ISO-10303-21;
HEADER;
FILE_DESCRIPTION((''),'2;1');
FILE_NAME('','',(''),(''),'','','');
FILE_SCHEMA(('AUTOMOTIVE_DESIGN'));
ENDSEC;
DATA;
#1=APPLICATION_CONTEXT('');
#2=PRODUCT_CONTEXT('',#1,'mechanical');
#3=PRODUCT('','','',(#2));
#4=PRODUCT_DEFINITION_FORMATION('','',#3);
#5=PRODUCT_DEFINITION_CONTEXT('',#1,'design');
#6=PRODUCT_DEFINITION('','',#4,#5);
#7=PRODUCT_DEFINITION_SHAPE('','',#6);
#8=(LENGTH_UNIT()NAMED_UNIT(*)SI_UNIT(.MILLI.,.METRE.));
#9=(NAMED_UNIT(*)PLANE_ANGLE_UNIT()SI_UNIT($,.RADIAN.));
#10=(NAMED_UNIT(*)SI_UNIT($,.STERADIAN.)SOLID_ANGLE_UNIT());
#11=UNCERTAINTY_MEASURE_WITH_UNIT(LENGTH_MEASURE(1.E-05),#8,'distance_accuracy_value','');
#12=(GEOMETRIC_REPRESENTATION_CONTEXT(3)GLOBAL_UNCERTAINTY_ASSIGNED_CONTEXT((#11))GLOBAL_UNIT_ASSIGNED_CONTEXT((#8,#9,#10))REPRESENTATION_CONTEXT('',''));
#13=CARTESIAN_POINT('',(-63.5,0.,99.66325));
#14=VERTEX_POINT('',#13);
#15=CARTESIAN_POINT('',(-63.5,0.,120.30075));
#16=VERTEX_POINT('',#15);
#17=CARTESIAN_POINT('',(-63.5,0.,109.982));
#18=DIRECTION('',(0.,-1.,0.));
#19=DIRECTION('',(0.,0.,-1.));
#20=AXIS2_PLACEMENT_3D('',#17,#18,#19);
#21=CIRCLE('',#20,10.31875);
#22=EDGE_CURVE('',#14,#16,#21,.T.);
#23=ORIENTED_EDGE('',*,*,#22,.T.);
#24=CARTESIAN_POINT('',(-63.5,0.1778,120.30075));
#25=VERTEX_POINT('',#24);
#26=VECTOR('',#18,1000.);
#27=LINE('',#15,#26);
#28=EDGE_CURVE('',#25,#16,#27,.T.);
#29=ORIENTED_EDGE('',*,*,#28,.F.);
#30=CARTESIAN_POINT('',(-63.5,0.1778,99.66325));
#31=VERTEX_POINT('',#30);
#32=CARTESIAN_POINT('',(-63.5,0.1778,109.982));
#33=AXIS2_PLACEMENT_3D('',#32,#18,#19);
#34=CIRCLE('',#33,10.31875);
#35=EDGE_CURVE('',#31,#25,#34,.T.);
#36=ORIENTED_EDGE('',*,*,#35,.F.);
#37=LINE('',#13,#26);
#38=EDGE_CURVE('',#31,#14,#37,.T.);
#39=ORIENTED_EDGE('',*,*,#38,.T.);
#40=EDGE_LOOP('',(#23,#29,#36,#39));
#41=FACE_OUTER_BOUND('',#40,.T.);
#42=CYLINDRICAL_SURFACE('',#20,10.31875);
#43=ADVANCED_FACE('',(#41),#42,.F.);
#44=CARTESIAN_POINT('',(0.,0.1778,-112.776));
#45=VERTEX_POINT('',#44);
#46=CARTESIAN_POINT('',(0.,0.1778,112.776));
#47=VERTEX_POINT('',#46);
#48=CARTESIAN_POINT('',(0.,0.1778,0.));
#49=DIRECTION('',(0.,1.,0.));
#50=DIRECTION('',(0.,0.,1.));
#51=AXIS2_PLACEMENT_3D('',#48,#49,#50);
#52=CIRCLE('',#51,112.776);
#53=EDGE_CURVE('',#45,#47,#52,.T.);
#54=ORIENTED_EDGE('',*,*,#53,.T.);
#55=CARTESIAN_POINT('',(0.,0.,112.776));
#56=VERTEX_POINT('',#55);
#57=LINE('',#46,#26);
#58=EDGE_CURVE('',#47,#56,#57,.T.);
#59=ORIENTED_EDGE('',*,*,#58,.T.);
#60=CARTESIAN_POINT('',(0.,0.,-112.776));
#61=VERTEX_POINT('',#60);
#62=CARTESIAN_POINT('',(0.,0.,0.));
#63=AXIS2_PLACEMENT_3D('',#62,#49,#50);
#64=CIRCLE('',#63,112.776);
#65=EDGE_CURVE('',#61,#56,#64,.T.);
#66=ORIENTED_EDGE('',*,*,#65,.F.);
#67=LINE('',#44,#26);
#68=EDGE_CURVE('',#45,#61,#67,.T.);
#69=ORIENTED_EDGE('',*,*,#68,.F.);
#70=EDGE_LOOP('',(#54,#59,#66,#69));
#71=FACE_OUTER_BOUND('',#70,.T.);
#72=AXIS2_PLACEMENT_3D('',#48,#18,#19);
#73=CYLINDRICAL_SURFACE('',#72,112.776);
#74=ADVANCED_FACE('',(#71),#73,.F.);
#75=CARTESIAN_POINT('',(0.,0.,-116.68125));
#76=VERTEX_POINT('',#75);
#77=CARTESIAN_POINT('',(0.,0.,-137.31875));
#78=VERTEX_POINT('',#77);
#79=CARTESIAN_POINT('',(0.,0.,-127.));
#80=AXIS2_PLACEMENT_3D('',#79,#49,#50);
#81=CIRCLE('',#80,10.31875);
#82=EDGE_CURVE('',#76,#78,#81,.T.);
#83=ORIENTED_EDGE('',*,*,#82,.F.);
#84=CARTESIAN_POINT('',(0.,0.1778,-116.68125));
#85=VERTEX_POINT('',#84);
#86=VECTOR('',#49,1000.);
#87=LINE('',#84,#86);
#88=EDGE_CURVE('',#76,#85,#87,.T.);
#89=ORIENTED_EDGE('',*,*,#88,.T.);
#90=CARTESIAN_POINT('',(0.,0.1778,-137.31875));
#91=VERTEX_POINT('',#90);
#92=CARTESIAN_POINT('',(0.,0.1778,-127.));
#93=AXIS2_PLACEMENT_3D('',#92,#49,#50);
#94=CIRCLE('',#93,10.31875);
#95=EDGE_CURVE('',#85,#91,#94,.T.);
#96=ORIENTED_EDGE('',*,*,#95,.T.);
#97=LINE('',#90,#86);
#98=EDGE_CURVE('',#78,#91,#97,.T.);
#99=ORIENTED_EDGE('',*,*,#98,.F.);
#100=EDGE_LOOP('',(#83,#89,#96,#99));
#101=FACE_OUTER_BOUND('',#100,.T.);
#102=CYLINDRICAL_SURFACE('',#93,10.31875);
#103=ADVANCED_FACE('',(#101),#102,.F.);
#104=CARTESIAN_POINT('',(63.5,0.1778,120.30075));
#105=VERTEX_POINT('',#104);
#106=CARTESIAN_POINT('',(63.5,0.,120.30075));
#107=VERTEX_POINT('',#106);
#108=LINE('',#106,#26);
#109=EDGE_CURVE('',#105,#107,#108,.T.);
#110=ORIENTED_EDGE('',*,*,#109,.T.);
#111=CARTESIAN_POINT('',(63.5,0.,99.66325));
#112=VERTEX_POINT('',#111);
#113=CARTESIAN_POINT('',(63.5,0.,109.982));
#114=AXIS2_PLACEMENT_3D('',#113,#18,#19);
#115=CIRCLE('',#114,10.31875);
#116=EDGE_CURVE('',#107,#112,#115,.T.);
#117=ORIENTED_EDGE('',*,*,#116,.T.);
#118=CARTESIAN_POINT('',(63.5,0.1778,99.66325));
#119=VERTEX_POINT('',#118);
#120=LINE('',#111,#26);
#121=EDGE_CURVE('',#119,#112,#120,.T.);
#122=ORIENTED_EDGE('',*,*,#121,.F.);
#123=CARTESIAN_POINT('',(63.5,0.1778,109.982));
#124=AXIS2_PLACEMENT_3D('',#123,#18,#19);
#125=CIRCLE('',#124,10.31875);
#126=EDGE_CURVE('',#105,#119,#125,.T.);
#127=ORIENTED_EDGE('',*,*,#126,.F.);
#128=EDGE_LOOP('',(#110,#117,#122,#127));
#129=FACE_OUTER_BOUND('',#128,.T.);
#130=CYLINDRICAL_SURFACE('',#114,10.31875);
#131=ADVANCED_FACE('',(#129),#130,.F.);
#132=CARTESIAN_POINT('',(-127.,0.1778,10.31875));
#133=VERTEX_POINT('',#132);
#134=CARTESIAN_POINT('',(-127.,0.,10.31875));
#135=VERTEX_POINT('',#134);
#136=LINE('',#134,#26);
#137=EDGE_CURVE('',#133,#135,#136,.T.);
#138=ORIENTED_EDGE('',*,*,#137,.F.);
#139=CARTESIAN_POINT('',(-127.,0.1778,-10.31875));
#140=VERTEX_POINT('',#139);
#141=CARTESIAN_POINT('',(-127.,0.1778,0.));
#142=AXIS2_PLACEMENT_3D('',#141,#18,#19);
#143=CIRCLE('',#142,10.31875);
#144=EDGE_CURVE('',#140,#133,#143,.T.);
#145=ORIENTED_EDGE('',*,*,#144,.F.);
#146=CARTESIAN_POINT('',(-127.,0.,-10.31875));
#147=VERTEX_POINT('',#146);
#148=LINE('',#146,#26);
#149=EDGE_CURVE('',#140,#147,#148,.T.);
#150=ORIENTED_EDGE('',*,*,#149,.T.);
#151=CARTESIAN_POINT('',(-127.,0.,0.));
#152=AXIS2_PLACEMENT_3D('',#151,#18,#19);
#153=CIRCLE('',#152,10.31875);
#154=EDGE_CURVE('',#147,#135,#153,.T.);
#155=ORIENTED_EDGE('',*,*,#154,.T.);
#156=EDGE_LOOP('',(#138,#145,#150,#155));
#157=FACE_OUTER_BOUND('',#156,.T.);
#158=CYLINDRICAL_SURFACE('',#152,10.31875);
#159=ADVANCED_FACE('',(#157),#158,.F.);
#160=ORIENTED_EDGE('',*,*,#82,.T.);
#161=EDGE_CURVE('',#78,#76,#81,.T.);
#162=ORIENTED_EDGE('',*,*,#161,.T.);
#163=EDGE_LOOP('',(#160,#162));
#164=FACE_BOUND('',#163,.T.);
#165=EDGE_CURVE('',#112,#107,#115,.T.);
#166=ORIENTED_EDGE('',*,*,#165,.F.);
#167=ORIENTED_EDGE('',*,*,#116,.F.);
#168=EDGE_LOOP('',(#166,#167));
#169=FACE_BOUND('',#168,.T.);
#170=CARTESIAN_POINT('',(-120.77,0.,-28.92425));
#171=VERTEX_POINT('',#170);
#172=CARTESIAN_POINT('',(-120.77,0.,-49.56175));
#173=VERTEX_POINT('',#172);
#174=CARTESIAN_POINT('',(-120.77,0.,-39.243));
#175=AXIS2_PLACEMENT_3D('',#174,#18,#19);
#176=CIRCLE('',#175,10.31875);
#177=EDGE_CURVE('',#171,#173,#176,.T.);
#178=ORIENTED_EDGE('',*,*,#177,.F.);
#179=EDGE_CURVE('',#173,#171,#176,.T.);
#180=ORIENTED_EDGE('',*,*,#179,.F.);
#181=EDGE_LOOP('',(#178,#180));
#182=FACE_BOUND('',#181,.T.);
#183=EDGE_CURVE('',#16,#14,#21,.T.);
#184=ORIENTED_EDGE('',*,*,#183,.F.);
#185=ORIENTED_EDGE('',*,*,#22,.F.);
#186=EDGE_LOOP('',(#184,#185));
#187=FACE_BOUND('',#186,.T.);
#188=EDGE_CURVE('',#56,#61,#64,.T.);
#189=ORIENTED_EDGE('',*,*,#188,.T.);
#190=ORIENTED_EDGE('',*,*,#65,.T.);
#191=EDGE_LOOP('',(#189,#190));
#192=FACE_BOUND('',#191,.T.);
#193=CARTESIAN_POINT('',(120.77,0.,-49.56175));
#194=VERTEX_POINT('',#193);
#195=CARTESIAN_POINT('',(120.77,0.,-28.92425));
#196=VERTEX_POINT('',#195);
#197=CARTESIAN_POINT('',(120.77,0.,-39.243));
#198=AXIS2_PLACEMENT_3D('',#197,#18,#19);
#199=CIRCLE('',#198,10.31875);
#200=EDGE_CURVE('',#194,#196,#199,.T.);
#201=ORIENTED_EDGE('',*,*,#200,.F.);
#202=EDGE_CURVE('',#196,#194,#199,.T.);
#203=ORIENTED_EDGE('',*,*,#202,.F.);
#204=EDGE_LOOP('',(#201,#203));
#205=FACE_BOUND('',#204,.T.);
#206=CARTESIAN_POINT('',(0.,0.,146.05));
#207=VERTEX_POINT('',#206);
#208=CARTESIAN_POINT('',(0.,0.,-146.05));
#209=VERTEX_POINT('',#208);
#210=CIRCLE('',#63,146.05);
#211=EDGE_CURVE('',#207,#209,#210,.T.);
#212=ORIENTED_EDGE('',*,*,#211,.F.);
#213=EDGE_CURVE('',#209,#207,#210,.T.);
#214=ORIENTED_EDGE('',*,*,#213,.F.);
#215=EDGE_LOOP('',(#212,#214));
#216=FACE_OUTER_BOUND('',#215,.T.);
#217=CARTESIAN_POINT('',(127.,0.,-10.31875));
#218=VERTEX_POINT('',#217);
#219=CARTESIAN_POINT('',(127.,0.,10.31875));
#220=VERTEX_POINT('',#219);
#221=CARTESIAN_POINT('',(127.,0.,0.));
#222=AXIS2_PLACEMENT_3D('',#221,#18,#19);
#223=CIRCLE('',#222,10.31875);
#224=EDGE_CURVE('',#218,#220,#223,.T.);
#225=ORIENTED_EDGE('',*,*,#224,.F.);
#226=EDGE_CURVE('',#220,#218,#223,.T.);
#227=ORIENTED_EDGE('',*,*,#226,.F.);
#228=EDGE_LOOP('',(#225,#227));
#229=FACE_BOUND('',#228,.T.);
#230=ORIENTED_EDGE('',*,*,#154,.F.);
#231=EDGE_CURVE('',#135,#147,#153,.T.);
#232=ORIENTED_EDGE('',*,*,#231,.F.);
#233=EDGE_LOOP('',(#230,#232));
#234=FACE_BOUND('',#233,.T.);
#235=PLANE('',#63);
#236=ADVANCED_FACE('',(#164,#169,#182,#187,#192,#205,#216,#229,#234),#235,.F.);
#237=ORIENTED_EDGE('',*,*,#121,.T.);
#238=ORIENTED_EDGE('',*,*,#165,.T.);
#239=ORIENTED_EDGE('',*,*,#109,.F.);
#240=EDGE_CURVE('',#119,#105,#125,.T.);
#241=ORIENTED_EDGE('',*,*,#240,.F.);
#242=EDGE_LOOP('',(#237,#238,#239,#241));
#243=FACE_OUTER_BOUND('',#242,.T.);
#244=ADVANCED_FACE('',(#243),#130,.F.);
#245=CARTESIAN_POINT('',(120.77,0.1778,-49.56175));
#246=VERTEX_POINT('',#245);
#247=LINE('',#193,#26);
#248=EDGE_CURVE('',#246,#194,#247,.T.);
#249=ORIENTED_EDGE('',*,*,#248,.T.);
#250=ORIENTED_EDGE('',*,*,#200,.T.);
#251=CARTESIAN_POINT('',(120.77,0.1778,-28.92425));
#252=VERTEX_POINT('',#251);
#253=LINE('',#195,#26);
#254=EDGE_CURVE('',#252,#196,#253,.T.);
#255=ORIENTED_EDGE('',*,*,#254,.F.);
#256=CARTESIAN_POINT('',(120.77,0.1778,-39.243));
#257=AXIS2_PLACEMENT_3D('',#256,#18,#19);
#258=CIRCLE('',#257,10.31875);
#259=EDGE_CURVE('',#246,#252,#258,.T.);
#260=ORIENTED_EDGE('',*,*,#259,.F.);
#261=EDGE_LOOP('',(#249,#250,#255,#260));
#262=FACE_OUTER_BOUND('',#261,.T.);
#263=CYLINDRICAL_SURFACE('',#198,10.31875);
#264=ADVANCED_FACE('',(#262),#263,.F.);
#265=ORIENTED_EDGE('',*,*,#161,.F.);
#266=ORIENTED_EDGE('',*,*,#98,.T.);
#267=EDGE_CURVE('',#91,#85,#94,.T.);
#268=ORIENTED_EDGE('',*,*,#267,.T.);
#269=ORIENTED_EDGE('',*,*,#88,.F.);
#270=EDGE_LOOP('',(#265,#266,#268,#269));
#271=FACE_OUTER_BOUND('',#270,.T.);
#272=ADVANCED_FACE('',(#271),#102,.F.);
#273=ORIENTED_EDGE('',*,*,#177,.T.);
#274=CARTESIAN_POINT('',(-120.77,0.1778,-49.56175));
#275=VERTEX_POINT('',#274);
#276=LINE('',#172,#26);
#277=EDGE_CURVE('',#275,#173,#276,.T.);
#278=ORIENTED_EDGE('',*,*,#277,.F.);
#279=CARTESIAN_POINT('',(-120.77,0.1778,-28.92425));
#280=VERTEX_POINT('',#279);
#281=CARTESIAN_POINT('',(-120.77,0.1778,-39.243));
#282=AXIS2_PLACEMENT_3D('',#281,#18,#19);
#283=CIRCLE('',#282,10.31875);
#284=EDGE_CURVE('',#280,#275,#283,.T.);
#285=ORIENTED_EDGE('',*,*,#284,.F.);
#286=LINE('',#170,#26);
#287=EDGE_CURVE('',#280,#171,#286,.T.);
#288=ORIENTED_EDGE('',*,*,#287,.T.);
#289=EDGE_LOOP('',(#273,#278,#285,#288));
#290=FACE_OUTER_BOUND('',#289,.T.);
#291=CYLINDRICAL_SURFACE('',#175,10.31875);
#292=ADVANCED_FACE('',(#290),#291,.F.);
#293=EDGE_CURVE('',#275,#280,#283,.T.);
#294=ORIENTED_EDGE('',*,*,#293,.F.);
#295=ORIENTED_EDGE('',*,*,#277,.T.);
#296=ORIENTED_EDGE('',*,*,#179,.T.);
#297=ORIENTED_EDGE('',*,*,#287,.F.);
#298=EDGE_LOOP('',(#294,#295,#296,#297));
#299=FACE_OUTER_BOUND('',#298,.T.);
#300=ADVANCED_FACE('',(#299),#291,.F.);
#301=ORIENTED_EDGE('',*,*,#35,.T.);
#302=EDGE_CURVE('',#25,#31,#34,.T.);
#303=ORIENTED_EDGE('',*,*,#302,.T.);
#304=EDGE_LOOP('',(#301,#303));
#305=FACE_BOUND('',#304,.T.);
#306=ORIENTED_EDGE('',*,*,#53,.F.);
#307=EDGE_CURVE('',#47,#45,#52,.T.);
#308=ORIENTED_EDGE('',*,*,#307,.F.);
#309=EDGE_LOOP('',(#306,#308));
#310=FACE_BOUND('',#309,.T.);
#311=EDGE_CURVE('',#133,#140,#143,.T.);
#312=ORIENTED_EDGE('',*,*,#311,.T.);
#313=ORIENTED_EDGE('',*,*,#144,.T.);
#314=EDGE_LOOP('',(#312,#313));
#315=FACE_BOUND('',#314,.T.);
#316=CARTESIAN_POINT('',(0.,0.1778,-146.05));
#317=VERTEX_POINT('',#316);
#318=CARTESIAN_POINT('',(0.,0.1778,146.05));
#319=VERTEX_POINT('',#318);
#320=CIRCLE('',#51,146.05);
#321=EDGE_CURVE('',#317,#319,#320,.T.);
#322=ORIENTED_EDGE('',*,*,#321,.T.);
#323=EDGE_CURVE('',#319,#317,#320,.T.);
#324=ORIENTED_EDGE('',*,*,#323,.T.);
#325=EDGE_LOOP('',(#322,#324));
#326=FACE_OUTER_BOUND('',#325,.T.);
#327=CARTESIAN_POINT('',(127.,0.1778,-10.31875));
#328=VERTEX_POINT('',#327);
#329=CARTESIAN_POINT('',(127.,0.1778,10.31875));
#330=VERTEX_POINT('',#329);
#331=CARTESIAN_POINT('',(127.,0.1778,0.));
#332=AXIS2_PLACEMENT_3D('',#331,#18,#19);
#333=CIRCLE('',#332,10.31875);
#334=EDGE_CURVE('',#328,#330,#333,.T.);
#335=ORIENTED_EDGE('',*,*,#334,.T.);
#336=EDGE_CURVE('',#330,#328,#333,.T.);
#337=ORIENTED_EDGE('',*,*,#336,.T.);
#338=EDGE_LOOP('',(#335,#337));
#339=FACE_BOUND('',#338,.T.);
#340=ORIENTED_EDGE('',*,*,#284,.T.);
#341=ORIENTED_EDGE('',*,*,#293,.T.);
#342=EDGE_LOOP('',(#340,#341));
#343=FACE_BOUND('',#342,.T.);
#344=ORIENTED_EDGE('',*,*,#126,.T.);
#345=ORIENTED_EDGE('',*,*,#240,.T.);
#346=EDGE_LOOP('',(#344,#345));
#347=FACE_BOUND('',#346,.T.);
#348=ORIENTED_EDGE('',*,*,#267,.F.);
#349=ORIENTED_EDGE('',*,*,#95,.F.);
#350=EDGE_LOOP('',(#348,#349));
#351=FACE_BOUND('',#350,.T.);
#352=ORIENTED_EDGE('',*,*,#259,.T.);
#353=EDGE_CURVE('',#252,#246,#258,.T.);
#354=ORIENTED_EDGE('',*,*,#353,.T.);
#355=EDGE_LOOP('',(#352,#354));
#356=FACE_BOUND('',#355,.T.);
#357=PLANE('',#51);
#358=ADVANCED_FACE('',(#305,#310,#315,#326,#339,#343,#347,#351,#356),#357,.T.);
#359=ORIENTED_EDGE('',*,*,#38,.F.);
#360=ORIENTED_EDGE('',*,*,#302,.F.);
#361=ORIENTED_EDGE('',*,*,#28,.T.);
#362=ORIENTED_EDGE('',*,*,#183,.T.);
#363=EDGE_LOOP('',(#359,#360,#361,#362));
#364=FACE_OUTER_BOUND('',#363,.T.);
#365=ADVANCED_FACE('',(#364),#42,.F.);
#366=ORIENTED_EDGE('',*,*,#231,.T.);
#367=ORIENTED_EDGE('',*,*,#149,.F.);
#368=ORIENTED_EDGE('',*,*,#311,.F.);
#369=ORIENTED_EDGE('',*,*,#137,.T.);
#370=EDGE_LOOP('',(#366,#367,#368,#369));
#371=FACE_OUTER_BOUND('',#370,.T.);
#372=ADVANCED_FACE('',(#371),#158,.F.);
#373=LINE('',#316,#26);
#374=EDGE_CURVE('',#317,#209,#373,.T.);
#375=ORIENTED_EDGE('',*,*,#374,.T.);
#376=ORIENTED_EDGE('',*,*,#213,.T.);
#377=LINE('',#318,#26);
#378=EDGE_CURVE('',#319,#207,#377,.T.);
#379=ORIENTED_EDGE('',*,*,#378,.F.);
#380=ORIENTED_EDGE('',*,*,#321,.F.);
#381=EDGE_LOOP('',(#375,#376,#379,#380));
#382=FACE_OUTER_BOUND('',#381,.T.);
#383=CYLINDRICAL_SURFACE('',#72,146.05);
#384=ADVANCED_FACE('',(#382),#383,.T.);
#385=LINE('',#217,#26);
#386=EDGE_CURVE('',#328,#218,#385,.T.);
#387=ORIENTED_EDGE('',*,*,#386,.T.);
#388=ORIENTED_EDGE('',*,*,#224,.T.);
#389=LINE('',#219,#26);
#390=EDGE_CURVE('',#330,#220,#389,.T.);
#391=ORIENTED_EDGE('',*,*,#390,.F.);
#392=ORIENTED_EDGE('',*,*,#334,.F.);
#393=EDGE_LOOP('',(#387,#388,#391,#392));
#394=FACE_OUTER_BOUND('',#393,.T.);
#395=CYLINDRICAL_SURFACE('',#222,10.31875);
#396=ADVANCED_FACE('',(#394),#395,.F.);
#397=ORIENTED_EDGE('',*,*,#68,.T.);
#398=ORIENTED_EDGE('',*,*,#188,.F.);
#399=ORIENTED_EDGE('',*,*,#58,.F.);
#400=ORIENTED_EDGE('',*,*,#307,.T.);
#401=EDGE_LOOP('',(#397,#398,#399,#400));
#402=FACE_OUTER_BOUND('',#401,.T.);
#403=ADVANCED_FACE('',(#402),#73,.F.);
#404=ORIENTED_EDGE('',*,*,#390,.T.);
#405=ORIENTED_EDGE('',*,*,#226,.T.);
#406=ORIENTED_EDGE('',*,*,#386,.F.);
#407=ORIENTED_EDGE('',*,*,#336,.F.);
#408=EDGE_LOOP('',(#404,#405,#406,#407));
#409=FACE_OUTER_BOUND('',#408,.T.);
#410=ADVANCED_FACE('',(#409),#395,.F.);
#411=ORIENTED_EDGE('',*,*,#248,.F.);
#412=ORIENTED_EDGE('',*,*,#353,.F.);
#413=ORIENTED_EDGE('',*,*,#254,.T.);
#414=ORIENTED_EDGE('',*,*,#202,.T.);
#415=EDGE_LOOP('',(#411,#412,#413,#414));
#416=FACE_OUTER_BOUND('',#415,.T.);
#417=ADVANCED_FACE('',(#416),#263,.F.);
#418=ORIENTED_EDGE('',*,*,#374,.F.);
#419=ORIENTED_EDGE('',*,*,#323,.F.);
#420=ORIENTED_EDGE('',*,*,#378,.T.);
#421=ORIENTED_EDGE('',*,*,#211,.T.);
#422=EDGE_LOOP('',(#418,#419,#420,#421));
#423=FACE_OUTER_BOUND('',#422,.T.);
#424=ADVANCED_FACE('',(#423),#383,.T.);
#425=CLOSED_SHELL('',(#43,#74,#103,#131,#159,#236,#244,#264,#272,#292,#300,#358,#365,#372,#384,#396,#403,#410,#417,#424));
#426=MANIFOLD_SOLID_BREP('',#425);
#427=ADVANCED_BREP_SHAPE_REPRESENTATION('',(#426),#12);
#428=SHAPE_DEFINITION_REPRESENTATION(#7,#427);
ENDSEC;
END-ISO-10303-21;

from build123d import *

# Parameters (mm, degrees)
SKETCH1_R                       = 146.05
SKETCH1_R_2                     = 112.776
BOSS_EXTRUDE1_DEPTH             = 0.1778
F_13_16_0_8125_DIAMETER_HOLE1_D = 20.6375
F_13_16_0_8125_DIAMETER_HOLE2_D = 20.6375


with BuildPart() as part:
    # Sketch1 → Boss-Extrude1 (new body)
    with BuildSketch(Plane(origin=(0, 0, 0), x_dir=(1, 0, 0), z_dir=(0, 1, 0))):
        with Locations(Location((0, 0, 0), (0, 0, 270))):
            Circle(SKETCH1_R)
        with Locations(Location((0, 0, 0), (0, 0, 270))):
            Circle(SKETCH1_R_2, mode=Mode.SUBTRACT)
    extrude(amount=BOSS_EXTRUDE1_DEPTH)

    # 13/16 (0.8125) Diameter Hole1 (through all)
    with Locations(Plane(origin=(0, 0.1778, 0), x_dir=(1, 0, 0), z_dir=(0, 1, 0))):
        with Locations((0, 127)):
            Hole(F_13_16_0_8125_DIAMETER_HOLE1_D / 2)

    # 13/16 (0.8125) Diameter Hole2 (through all)
    with Locations(Plane(origin=(0, 0, 0), x_dir=(-1, 0, 0), z_dir=(0, -1, 0))):
        with Locations((-63.5, -109.982), (-120.77, 39.243), (-127, 0)):
            f_13_16_0_8125_diameter_hole2 = Hole(F_13_16_0_8125_DIAMETER_HOLE2_D / 2)

    # Mirror1: 13/16 (0.8125) Diameter Hole2 across plane
    add(f_13_16_0_8125_diameter_hole2.mirror(Plane(origin=(0, 0, 0), x_dir=(0, 0, 1), z_dir=(1, 0, 0))), mode=Mode.SUBTRACT)


solid = part.part
